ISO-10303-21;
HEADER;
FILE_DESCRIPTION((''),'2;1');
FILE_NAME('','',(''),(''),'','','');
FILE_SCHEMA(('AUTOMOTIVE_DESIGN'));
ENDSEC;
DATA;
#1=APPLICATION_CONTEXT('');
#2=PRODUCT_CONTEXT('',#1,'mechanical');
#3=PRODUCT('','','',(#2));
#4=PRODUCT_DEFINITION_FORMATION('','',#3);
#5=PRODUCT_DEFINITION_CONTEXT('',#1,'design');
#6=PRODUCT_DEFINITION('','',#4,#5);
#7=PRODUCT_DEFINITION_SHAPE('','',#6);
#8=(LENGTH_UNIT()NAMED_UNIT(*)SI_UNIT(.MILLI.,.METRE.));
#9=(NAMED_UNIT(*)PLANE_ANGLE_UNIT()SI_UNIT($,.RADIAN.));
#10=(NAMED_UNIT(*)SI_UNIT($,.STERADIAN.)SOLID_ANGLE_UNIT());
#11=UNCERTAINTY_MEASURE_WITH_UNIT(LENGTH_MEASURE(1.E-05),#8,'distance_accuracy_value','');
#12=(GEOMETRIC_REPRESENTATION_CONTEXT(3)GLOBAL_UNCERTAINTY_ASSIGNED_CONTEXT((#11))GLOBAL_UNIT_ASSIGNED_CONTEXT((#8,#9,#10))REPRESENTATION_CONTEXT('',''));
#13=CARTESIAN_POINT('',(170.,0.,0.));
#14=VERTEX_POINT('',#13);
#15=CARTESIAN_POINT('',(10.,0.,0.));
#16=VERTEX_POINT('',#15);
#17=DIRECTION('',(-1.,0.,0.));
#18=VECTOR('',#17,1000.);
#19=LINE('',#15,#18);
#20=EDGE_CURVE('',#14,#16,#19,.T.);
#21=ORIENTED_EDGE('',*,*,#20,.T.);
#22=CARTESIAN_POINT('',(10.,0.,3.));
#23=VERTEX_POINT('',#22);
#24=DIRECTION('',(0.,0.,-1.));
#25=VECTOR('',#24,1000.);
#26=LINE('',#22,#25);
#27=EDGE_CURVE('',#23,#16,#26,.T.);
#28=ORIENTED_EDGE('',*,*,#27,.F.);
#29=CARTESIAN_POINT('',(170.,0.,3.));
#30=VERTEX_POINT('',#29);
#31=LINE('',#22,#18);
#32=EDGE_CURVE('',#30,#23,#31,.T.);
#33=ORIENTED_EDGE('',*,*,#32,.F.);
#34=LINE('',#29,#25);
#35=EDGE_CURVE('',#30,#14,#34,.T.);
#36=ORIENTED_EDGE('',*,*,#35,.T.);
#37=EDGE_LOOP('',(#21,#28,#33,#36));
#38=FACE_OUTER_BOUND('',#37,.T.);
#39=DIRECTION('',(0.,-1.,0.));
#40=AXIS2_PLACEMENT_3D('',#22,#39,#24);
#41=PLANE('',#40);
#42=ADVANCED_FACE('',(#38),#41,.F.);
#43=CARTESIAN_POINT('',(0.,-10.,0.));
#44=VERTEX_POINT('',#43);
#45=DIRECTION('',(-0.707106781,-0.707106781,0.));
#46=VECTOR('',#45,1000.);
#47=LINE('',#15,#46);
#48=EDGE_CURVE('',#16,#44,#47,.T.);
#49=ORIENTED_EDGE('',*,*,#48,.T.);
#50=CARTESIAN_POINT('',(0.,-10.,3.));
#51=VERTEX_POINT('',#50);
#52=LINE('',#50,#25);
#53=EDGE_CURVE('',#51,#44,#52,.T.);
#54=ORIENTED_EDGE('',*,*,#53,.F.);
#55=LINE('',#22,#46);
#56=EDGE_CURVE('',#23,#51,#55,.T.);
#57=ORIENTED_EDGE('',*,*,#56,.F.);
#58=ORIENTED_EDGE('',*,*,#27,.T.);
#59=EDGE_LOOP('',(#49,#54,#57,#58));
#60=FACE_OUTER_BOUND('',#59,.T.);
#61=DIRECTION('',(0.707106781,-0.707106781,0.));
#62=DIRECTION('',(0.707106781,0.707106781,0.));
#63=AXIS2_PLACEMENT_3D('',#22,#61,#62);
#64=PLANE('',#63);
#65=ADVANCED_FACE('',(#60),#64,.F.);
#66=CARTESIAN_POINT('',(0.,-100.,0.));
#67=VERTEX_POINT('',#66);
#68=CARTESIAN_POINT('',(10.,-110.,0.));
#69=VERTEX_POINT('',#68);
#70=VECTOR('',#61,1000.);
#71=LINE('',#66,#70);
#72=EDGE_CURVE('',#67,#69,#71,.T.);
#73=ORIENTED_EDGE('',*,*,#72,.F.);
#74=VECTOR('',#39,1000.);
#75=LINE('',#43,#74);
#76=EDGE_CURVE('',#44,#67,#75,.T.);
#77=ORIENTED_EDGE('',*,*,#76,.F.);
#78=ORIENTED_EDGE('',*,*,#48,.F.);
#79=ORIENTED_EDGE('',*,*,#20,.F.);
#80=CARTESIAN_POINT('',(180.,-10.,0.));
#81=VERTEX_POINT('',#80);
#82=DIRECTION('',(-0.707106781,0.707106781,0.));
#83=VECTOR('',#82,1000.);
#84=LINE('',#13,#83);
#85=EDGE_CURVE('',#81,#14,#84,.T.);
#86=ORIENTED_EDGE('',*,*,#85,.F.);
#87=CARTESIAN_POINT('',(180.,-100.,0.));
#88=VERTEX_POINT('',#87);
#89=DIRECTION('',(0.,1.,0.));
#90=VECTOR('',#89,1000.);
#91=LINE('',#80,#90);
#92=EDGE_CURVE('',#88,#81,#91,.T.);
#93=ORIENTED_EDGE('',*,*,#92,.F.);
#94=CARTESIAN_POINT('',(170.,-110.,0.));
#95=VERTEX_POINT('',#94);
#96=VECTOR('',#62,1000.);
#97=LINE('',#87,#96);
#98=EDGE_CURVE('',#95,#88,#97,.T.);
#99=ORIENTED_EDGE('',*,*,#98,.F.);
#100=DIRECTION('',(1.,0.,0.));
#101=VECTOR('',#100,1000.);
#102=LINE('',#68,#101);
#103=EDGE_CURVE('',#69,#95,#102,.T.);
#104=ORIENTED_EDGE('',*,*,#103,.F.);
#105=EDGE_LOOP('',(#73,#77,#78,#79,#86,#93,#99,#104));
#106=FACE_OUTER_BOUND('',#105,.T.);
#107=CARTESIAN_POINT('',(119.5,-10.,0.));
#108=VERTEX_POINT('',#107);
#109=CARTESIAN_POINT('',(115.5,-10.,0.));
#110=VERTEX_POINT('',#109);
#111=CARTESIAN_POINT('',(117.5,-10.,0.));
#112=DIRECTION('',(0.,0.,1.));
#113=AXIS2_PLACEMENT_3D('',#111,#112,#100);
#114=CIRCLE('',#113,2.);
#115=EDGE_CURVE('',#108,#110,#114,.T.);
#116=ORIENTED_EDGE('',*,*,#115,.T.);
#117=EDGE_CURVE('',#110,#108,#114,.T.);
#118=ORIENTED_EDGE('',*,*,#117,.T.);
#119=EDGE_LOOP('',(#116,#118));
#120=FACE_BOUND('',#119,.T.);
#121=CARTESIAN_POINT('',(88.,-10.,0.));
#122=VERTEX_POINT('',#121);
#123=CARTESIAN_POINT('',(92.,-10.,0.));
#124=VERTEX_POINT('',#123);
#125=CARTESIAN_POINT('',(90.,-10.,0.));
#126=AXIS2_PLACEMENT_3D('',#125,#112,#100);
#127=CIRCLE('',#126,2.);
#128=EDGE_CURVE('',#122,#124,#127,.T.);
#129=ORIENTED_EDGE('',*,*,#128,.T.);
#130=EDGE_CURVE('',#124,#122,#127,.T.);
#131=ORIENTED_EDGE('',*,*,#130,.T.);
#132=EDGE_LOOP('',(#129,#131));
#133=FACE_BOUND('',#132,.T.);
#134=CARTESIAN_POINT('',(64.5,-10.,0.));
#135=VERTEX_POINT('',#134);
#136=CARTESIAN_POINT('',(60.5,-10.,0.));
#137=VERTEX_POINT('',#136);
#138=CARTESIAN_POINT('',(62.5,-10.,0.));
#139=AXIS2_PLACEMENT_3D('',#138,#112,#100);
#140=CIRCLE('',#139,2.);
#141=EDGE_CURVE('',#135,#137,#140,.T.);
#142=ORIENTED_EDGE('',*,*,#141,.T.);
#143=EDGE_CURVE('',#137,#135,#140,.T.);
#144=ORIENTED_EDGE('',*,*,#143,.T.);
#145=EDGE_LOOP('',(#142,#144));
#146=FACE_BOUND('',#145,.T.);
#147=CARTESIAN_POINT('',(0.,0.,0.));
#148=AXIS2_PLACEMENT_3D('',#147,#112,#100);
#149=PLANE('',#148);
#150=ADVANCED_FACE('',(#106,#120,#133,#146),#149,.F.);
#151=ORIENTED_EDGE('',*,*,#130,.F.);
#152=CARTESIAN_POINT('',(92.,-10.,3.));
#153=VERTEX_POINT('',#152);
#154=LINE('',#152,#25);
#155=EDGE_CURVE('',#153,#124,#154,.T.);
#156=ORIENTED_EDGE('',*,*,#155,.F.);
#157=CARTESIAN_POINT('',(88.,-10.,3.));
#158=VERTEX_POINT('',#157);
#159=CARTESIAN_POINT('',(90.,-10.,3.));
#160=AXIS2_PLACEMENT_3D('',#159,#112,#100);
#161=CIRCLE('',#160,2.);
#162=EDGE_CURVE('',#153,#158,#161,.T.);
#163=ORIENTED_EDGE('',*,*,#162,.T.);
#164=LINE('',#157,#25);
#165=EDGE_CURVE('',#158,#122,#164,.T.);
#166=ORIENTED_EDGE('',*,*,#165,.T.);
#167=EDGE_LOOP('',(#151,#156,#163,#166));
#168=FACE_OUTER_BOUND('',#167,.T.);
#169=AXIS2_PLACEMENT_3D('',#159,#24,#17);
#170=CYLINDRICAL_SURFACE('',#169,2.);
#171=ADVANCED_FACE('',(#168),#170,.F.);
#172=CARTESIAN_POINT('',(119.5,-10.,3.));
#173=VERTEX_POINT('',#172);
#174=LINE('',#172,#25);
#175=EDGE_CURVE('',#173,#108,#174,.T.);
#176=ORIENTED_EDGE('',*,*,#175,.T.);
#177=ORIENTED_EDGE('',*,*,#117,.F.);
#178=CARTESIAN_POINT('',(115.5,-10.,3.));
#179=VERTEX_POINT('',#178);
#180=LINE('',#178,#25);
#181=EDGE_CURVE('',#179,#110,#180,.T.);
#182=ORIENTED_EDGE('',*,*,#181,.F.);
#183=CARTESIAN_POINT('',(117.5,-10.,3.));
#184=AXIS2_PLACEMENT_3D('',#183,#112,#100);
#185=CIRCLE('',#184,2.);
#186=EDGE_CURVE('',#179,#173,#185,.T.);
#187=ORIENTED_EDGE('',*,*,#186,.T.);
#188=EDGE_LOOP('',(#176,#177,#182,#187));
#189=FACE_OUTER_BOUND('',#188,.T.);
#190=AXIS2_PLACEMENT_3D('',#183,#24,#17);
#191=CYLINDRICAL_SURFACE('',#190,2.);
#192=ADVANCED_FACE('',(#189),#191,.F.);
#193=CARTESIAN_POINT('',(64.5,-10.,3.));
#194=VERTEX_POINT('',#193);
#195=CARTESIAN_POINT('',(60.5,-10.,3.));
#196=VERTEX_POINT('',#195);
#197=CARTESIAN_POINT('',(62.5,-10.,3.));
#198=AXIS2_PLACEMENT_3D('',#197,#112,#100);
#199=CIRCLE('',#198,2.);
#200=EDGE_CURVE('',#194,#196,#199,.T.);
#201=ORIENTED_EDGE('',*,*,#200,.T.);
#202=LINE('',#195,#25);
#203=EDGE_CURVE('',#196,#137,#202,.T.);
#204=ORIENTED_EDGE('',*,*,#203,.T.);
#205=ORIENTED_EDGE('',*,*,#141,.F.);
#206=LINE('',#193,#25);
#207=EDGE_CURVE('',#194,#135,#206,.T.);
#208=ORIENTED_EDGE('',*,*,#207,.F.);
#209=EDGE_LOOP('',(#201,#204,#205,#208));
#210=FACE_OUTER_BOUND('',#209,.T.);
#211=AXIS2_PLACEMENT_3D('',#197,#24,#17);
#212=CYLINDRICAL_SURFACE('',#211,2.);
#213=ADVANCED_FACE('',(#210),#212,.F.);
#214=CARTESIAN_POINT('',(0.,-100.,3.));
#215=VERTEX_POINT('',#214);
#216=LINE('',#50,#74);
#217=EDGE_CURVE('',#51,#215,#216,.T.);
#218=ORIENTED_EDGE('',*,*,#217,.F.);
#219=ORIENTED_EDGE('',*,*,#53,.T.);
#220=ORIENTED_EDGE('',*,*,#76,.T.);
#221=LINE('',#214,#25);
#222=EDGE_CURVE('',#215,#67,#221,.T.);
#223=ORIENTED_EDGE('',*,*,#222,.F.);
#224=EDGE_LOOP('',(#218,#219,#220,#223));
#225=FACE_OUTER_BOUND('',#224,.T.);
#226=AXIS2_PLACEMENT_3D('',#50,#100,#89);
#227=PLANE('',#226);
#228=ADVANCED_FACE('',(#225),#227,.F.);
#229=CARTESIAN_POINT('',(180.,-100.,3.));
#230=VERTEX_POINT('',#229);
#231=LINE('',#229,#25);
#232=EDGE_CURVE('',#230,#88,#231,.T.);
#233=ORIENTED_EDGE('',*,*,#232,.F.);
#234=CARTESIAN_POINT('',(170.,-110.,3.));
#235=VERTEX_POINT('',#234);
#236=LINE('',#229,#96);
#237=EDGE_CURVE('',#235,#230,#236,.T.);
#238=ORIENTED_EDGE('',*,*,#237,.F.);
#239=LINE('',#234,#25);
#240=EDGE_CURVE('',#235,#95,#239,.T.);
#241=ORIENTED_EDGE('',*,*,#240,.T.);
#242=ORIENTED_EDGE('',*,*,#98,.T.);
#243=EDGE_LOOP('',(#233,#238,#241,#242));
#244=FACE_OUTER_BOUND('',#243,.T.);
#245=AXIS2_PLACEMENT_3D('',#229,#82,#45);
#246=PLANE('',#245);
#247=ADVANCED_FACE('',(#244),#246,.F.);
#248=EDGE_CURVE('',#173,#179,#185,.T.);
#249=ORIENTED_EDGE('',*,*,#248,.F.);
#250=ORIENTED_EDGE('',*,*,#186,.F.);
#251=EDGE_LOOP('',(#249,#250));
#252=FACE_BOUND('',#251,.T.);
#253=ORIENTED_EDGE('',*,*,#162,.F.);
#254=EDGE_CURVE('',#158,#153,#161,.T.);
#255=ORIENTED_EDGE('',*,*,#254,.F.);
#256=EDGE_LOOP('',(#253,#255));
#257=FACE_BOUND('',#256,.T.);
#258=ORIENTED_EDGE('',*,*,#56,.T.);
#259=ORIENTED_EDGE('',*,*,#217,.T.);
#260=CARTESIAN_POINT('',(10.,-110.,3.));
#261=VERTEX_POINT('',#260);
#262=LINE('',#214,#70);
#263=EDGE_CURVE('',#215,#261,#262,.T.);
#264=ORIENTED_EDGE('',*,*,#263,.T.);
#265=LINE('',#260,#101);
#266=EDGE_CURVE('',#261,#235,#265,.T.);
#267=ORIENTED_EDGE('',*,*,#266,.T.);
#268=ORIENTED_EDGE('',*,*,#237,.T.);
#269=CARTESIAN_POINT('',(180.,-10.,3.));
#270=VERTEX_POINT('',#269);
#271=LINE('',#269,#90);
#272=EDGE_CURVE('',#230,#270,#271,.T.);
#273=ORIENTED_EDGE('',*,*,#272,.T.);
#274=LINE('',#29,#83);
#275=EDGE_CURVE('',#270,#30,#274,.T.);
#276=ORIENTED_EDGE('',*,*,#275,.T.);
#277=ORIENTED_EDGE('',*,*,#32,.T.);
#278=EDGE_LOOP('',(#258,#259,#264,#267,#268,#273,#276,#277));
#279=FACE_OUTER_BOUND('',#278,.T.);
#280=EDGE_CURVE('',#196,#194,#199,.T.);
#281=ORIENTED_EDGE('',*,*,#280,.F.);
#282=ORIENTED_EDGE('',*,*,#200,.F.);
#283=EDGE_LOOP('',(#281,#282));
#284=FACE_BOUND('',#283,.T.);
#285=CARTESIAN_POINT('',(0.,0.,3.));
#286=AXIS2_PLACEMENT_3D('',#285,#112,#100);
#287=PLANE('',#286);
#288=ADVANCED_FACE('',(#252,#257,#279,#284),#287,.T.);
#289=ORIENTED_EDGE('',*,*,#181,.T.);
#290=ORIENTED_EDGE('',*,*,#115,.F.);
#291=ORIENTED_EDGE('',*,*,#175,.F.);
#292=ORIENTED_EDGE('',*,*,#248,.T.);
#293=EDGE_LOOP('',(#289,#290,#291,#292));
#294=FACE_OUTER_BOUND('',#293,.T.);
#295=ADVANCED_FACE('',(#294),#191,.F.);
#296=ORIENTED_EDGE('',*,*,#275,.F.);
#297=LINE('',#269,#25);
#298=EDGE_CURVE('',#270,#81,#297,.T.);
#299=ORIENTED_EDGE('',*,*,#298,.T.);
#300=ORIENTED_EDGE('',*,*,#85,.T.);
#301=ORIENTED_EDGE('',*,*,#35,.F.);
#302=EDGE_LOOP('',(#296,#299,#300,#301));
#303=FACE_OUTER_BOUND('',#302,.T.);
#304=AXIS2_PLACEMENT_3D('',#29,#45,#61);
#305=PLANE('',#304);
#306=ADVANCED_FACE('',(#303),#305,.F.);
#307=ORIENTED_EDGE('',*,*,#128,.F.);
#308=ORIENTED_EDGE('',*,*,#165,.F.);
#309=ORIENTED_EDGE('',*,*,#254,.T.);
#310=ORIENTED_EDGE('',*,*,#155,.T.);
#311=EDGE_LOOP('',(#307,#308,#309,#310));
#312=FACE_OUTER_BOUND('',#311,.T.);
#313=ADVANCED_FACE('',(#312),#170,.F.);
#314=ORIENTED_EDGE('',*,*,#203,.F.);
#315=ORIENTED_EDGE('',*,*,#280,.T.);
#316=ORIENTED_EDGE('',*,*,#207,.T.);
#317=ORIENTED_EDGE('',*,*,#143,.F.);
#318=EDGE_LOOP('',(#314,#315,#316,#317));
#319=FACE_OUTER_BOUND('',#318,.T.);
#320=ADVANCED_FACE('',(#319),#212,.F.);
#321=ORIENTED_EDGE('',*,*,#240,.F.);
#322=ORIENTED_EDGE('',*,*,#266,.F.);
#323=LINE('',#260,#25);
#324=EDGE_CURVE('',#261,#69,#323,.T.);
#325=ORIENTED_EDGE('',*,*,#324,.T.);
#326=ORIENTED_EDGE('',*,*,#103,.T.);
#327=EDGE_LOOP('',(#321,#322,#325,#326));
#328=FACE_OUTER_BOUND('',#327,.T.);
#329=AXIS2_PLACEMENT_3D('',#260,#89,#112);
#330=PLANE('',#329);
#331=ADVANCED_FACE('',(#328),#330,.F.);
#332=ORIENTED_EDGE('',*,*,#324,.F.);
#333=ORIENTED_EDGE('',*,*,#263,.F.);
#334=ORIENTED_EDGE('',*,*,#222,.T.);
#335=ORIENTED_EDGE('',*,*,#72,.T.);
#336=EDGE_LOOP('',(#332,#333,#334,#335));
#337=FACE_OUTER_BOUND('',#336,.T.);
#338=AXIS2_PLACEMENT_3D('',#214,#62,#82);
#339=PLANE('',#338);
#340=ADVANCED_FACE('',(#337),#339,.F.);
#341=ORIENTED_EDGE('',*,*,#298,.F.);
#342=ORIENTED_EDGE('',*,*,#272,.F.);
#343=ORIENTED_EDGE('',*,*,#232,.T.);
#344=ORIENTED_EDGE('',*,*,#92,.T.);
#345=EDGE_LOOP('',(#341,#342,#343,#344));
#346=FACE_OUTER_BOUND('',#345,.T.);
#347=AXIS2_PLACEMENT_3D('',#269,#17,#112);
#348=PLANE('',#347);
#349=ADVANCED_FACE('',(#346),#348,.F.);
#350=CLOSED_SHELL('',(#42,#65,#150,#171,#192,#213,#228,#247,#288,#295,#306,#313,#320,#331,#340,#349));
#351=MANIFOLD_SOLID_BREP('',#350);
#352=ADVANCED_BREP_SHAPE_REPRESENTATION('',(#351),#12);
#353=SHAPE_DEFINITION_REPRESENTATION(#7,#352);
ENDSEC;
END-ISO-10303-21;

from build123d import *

# Parameters (mm, degrees)
SKETCH1_R           = 2
BOSS_EXTRUDE1_DEPTH = 3


with BuildPart() as part:
    # Sketch1 → Boss-Extrude1 (new body)
    with BuildSketch(Plane.XY):
        Polygon((10, 0), (170, 0), (180, -10), (180, -100), (170, -110), (10, -110), (0, -100), (0, -10), align=None)
        with Locations((90, -10)):
            Circle(SKETCH1_R, mode=Mode.SUBTRACT)
        with Locations((117.5, -10)):
            Circle(SKETCH1_R, mode=Mode.SUBTRACT)
        with Locations((62.5, -10)):
            Circle(SKETCH1_R, mode=Mode.SUBTRACT)
    extrude(amount=BOSS_EXTRUDE1_DEPTH)


solid = part.part
